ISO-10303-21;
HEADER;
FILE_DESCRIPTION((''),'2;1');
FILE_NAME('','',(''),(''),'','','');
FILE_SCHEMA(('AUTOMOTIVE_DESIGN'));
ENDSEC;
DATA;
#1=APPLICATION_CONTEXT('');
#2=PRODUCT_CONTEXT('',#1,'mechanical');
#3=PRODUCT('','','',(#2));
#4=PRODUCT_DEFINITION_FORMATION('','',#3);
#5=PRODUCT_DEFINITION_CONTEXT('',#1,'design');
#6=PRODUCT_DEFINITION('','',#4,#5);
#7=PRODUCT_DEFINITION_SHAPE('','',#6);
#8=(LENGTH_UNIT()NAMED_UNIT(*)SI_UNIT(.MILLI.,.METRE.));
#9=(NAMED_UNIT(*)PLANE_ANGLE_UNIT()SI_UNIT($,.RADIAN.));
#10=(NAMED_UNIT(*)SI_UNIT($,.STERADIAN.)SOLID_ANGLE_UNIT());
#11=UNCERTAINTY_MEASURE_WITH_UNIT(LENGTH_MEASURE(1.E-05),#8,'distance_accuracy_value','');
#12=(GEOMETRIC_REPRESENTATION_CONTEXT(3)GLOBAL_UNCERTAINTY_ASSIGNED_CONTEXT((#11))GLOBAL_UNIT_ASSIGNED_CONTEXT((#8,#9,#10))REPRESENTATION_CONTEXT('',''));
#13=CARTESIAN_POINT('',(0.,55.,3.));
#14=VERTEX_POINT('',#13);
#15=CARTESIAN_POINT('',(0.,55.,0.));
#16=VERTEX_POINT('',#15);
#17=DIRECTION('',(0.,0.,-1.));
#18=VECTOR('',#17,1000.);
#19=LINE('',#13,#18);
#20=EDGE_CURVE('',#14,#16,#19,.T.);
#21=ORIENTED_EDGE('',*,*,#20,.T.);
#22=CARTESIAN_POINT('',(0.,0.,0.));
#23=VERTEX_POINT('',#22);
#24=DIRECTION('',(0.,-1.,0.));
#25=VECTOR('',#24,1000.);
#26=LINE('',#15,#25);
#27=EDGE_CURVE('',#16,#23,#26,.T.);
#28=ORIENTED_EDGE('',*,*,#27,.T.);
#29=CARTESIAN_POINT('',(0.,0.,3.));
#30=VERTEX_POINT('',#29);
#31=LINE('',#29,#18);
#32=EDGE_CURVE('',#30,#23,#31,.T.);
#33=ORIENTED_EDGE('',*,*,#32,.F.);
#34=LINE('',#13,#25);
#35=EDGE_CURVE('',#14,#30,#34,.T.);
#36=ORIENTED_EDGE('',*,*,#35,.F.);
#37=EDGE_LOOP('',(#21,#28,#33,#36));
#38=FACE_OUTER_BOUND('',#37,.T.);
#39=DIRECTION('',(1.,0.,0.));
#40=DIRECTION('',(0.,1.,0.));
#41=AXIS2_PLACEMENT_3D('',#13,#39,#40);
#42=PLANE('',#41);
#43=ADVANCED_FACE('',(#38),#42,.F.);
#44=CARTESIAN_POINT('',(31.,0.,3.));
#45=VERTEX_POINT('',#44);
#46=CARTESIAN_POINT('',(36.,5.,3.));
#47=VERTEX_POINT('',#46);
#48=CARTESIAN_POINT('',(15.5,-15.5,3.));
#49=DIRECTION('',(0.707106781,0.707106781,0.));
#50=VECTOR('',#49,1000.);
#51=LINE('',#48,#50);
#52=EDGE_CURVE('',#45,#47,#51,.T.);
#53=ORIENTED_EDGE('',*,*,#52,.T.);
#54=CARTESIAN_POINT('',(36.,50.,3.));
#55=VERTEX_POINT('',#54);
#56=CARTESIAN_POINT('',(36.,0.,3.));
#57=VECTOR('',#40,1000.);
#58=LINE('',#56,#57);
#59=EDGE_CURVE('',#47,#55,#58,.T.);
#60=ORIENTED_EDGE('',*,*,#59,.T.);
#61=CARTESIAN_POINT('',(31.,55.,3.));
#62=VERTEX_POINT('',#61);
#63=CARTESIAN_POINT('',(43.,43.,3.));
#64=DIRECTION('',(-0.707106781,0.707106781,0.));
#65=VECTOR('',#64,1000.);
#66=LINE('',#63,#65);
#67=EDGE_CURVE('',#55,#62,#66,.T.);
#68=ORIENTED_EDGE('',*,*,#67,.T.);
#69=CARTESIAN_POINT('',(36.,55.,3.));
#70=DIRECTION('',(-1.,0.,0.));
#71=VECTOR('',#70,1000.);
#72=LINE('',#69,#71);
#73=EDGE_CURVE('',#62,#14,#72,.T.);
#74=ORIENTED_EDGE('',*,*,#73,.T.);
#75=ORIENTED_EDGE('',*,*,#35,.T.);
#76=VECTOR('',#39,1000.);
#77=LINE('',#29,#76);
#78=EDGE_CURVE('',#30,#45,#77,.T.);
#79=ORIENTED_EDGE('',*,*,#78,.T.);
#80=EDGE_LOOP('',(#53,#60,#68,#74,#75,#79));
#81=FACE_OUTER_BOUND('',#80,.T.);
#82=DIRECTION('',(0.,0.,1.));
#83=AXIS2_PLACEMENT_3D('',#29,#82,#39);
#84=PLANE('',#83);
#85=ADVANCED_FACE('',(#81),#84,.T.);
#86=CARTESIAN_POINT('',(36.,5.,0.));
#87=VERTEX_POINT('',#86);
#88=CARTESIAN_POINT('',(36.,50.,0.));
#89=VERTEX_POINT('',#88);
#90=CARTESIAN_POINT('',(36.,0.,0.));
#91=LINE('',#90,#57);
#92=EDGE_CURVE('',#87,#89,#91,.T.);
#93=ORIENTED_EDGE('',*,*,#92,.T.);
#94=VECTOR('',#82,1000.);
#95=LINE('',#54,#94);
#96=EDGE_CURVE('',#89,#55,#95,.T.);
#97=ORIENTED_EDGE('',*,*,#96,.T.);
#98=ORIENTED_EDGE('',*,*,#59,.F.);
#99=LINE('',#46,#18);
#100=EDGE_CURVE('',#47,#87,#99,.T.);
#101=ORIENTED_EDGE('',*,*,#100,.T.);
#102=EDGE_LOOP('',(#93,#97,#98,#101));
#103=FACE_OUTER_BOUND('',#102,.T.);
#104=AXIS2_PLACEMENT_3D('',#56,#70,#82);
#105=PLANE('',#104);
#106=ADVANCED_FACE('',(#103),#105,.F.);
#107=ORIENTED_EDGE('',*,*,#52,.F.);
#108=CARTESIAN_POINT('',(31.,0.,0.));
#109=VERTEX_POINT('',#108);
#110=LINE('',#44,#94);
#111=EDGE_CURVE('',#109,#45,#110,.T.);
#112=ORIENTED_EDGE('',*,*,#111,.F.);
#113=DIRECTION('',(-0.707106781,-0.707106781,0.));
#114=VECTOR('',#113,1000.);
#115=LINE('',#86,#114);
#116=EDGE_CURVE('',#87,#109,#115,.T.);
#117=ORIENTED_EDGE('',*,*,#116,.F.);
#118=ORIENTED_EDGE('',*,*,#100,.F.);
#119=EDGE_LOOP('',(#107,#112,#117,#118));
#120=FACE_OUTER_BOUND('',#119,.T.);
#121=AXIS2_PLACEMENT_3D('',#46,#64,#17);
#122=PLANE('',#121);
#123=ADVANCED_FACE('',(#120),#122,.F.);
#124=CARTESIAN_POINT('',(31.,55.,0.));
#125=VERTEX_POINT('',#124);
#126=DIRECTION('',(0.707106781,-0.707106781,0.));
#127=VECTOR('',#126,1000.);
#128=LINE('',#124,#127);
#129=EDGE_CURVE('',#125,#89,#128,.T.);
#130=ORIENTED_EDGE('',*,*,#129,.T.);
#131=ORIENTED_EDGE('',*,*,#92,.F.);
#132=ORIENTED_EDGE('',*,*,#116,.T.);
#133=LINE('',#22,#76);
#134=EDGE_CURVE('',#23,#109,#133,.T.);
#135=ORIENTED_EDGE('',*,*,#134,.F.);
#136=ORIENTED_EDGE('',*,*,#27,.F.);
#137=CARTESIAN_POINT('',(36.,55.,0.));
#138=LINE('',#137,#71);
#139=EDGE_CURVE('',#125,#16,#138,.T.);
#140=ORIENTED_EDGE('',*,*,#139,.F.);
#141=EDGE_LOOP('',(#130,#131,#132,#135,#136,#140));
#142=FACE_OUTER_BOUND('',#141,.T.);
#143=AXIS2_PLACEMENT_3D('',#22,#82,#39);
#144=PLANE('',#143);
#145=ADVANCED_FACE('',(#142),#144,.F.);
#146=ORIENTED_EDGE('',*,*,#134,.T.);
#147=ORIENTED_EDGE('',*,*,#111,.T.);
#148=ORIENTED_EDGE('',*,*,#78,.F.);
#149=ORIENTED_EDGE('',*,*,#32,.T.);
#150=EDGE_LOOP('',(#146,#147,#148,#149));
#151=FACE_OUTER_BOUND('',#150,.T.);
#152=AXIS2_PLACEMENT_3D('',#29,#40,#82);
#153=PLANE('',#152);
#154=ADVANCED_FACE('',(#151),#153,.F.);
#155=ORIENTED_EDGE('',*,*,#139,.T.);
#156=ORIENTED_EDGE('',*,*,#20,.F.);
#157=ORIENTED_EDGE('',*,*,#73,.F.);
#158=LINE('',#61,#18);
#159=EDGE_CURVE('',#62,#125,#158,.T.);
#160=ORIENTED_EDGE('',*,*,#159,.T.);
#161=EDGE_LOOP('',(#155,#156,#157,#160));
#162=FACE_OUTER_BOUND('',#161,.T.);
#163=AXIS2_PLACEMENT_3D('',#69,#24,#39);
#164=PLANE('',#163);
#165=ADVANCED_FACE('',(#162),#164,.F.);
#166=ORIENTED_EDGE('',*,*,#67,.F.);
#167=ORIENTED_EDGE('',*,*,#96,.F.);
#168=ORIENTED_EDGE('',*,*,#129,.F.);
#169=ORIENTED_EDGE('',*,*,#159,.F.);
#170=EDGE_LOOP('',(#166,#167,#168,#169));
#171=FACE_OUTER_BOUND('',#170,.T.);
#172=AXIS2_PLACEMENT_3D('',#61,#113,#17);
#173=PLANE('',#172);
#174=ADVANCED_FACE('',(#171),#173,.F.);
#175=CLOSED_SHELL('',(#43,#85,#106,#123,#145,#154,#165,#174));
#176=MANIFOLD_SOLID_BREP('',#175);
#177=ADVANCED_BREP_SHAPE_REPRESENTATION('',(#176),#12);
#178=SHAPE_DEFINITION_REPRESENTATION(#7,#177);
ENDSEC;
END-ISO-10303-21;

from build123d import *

# Parameters (mm, degrees)
SKETCH_1_W      = 36
SKETCH_1_H      = 55
EXTRUDE_1_DEPTH = 3
CHAMFER_1_SIZE  = 5


with BuildPart() as part:
    # 草图1 → 凸台-拉伸1 (new body)
    with BuildSketch(Plane.XY):
        with Locations((18, 27.5)):
            Rectangle(SKETCH_1_W, SKETCH_1_H)
    extrude(amount=EXTRUDE_1_DEPTH)

    # 倒角1
    chamfer_1_edges = [part.edges().sort_by_distance(p)[0] for p in [
        (36, 55, 1.5),
        (36, 0, 1.5),
    ]]
    chamfer(chamfer_1_edges, length=CHAMFER_1_SIZE)


solid = part.part
